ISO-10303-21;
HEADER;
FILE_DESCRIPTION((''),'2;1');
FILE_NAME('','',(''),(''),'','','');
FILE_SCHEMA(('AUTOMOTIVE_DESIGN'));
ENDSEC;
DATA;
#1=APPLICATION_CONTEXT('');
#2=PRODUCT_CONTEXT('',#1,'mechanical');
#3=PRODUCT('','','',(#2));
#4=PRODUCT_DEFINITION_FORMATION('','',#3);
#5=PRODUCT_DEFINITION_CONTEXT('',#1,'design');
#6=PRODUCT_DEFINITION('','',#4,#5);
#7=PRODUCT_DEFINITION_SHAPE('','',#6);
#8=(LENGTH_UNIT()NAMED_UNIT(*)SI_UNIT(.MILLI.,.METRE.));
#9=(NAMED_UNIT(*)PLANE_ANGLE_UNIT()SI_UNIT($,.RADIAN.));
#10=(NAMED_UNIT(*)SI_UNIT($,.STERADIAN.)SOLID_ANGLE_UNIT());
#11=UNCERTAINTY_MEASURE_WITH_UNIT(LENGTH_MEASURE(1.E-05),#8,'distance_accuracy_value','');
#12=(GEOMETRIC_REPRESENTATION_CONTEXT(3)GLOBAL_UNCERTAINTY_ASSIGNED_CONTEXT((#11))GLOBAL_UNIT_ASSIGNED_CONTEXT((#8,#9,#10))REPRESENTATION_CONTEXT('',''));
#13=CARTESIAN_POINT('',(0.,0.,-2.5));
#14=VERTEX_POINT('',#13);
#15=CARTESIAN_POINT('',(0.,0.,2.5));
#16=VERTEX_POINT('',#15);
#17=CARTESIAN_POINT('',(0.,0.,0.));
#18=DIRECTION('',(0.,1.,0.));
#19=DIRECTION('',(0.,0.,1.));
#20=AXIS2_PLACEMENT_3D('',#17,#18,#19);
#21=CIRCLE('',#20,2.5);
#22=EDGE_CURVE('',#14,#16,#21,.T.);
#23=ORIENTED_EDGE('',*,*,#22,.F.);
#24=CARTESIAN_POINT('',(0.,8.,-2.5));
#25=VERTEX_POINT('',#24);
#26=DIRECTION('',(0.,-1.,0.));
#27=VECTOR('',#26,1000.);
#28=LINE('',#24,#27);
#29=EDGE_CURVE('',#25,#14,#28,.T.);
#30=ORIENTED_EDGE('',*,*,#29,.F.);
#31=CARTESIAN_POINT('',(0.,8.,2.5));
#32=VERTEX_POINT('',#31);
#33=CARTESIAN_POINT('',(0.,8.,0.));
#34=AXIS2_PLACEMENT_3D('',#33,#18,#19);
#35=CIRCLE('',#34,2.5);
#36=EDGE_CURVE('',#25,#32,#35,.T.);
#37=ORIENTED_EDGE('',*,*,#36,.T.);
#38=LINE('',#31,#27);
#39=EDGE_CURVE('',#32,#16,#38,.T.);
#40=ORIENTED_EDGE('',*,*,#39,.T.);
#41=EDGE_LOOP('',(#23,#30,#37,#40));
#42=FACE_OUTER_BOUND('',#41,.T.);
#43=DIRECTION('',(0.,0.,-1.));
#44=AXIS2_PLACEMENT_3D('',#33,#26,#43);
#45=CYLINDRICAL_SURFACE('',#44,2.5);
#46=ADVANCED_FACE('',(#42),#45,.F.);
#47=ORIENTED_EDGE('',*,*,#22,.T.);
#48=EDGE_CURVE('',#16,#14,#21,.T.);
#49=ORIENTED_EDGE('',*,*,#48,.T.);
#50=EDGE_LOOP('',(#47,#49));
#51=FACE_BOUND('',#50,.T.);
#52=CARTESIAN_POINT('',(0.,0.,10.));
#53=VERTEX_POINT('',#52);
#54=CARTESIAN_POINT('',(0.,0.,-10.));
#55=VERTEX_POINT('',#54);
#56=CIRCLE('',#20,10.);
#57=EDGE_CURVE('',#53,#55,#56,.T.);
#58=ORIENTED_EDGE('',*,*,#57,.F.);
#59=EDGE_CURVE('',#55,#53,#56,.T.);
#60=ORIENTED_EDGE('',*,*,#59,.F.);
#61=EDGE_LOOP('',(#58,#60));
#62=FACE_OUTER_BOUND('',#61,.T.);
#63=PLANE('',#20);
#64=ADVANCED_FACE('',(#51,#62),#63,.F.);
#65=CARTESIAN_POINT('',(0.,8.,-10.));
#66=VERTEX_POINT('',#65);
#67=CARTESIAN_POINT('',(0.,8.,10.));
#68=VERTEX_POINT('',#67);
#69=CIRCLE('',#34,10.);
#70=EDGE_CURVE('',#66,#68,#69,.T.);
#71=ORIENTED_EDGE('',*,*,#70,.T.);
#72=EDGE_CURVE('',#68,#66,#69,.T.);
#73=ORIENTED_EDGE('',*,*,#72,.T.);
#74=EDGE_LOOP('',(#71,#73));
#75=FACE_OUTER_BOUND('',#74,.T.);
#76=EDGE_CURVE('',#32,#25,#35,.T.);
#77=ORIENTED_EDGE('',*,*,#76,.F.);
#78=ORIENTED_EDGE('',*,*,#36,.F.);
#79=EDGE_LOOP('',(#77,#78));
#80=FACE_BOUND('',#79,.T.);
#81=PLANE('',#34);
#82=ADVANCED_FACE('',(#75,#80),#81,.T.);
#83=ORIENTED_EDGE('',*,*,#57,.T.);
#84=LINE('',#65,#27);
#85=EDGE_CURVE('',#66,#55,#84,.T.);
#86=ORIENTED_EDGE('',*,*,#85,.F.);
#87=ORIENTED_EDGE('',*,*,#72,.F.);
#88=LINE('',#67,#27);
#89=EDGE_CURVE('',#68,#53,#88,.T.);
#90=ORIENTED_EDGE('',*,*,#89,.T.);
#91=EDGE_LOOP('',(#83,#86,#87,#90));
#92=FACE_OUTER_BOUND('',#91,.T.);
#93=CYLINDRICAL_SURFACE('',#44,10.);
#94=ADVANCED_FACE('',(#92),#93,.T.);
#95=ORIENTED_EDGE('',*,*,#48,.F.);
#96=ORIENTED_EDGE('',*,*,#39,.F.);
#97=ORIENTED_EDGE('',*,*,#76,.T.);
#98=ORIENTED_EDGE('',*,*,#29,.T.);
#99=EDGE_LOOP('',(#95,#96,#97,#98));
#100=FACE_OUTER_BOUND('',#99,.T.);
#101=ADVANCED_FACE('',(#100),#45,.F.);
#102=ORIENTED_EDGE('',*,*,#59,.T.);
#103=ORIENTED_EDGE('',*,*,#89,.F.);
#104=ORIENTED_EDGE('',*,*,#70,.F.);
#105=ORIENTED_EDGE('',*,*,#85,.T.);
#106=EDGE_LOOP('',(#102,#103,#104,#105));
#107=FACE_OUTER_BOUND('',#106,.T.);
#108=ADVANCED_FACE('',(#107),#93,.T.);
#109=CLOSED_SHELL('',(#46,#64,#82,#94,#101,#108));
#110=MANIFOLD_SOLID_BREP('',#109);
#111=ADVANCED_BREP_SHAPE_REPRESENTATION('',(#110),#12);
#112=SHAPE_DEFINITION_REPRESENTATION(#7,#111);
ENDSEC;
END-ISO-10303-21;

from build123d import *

# Parameters (mm, degrees)
SKETCH1_R           = 10
SKETCH1_R_2         = 2.5
BOSS_EXTRUDE1_DEPTH = 8


with BuildPart() as part:
    # Sketch1 → Boss-Extrude1 (new body)
    with BuildSketch(Plane(origin=(0, 0, 0), x_dir=(1, 0, 0), z_dir=(0, 1, 0))):
        with Locations(Location((0, 0, 0), (0, 0, 270))):
            Circle(SKETCH1_R)
        with Locations(Location((0, 0, 0), (0, 0, 270))):
            Circle(SKETCH1_R_2, mode=Mode.SUBTRACT)
    extrude(amount=BOSS_EXTRUDE1_DEPTH)


solid = part.part
